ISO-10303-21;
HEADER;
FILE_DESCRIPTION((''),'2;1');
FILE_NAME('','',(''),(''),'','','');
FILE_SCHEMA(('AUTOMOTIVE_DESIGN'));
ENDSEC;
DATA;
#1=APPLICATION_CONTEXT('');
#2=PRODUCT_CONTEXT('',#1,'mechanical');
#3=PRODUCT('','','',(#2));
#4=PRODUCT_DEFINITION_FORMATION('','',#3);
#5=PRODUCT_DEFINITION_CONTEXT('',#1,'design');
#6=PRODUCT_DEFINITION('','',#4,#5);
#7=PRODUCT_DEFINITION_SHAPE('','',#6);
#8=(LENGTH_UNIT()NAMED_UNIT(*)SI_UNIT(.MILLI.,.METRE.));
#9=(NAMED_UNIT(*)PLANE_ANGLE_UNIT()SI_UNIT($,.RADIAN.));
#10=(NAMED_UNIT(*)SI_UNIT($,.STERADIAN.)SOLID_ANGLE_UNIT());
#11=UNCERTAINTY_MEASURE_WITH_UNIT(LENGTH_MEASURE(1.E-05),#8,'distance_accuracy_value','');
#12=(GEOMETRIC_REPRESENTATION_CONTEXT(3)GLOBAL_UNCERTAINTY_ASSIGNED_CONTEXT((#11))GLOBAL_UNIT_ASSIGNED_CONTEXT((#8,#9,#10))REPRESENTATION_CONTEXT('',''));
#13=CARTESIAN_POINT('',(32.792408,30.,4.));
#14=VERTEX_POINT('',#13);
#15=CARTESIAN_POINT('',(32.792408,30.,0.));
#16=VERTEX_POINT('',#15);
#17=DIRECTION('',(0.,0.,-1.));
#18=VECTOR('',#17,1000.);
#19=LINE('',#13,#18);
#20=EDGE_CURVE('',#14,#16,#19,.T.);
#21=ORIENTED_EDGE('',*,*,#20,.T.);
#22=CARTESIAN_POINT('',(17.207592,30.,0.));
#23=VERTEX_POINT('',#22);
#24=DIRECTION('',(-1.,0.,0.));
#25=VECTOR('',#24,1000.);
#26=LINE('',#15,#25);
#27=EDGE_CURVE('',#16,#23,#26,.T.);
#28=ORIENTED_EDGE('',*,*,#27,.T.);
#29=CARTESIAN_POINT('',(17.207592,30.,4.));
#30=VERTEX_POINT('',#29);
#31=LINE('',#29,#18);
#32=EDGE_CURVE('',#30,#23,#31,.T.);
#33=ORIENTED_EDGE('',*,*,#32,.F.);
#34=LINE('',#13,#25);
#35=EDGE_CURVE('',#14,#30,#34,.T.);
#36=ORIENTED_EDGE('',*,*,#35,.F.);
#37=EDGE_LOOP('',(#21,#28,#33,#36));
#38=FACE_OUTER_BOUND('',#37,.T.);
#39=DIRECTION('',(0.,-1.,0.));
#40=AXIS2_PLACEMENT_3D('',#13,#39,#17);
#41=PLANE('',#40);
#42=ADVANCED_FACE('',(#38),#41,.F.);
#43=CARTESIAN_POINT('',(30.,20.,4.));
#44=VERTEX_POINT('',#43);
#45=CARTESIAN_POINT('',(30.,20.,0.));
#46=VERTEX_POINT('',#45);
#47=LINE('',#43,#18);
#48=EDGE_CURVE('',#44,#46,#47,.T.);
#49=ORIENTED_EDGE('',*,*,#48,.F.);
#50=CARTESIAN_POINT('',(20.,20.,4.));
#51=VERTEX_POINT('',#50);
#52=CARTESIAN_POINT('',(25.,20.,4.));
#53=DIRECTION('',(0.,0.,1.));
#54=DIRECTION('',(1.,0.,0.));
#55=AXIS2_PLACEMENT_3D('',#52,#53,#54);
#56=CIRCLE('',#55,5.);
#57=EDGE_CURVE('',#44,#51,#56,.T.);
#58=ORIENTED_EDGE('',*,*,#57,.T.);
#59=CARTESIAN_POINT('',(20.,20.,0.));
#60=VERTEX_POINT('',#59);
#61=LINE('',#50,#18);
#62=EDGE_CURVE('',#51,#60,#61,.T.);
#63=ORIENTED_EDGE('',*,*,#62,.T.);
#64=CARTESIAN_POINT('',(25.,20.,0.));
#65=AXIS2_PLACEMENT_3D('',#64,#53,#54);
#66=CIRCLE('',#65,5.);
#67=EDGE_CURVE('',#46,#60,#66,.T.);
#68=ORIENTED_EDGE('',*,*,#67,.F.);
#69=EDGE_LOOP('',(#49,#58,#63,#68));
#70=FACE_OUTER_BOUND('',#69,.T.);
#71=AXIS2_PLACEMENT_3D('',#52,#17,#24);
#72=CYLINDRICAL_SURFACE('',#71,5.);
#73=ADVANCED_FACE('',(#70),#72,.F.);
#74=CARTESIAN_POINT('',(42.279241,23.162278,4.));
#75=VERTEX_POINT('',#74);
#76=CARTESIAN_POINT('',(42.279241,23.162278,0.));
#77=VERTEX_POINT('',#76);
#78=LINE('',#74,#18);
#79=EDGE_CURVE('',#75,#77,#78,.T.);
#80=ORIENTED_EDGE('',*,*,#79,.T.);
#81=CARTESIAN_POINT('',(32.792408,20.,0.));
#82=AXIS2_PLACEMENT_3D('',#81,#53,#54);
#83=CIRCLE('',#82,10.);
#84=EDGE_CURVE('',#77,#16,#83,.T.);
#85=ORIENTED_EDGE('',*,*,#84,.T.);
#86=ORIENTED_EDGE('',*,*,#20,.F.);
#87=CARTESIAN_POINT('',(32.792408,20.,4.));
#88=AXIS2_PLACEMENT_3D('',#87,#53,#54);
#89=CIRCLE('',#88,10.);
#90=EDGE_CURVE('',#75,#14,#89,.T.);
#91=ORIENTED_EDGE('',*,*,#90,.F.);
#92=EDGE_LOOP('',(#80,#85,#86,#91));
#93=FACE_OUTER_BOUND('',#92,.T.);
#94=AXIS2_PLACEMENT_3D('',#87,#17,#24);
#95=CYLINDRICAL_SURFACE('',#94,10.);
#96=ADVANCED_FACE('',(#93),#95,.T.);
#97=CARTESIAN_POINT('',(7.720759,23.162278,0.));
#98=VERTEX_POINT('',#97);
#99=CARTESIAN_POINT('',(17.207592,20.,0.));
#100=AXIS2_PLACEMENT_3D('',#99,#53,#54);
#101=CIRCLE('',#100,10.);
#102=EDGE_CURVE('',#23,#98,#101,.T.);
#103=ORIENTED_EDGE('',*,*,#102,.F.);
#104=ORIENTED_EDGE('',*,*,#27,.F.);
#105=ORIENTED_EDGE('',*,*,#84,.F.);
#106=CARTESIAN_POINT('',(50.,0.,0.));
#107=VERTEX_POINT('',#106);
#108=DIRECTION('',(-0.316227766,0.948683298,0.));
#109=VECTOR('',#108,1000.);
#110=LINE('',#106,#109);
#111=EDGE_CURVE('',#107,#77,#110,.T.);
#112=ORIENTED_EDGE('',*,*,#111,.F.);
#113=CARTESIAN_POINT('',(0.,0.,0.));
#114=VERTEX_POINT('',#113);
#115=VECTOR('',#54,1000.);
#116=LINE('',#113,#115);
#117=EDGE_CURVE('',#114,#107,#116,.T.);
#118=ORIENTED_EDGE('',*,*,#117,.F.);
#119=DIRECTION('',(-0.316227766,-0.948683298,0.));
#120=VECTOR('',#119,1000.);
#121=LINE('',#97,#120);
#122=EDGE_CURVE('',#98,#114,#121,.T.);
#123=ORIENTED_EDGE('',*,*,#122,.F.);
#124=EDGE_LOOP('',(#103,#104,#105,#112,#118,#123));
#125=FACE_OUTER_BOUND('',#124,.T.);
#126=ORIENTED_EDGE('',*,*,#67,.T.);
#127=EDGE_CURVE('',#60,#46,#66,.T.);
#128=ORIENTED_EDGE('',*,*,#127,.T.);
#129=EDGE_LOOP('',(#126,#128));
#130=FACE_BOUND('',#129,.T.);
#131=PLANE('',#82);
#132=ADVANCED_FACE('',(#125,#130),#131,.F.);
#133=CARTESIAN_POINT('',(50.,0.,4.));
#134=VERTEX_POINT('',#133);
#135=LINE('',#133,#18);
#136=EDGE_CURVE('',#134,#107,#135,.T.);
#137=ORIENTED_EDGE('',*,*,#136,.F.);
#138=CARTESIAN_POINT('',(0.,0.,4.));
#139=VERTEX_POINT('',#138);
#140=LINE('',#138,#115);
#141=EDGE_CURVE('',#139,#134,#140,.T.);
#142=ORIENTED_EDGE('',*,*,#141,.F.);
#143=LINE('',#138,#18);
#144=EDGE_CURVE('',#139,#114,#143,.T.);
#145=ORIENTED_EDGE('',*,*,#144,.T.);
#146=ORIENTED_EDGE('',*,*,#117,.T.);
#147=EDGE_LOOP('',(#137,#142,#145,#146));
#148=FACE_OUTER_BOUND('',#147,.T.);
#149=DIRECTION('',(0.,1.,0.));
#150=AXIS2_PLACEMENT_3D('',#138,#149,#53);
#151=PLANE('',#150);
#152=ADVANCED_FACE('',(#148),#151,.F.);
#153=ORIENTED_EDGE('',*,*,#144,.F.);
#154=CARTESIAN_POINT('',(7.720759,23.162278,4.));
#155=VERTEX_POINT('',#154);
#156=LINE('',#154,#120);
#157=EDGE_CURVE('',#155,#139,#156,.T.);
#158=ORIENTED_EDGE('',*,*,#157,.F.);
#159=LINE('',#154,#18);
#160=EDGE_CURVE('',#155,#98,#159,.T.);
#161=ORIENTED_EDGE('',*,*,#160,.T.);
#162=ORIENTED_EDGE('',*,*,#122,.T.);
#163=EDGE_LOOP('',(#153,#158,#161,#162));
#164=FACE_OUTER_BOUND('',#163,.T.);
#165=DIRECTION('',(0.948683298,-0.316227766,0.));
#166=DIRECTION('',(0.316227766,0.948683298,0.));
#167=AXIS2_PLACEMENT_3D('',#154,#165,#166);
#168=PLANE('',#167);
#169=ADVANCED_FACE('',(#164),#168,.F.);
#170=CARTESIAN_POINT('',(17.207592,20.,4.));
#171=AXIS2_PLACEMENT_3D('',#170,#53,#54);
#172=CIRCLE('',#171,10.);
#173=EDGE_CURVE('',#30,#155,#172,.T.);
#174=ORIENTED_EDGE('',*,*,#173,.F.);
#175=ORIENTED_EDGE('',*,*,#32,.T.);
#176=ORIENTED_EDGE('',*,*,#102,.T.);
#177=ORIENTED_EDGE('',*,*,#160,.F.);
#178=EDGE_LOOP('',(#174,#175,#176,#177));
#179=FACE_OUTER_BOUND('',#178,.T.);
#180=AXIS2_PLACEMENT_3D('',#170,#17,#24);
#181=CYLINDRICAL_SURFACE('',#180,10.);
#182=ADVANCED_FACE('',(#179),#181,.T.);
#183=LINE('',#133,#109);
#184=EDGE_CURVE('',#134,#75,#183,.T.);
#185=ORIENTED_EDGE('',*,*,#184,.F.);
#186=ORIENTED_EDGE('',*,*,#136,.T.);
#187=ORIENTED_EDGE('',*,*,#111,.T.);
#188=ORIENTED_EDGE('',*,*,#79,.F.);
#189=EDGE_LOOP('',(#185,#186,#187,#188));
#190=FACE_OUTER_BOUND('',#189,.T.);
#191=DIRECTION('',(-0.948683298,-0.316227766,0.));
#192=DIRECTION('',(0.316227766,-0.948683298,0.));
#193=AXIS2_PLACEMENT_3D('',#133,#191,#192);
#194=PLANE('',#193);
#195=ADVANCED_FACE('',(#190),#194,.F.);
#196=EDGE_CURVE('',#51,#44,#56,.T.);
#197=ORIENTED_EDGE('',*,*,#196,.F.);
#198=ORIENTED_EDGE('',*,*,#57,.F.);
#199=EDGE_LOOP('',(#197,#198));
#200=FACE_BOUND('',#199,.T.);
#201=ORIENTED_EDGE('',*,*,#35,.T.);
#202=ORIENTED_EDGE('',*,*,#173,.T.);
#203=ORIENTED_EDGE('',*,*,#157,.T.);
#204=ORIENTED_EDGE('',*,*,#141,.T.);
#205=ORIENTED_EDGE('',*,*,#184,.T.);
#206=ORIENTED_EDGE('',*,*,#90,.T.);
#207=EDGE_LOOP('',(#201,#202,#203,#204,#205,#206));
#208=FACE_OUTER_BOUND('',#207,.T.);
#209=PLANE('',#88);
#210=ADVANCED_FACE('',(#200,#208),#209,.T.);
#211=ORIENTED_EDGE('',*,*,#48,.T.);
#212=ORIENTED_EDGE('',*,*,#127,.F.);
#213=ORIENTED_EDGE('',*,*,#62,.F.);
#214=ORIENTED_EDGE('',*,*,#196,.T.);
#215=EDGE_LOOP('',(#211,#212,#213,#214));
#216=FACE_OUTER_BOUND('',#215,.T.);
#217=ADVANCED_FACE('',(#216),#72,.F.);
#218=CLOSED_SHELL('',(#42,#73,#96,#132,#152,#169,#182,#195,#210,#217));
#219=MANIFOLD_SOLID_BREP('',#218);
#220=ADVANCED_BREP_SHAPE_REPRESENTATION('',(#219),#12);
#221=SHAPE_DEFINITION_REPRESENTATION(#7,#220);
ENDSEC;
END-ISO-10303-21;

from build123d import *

# Parameters (mm, degrees)
SKETCH1_R           = 5
BOSS_EXTRUDE1_DEPTH = 4


with BuildPart() as part:
    # Sketch1 → Boss-Extrude1 (new body)
    with BuildSketch(Plane.XY):
        with BuildLine():
            Line((0, 0), (50, 0))
            Line((50, 0), (42.27924078, 23.16227766))
            ThreePointArc((42.27924078, 23.16227766), (38.639510646, 28.112421852), (32.792407799, 30))
            Line((32.792407799, 30), (17.207592201, 30))
            ThreePointArc((17.207592201, 30), (11.360489354, 28.112421852), (7.72075922, 23.16227766))
            Line((7.72075922, 23.16227766), (0, 0))
        make_face()
        with Locations((25, 20)):
            Circle(SKETCH1_R, mode=Mode.SUBTRACT)
    extrude(amount=BOSS_EXTRUDE1_DEPTH)


solid = part.part
